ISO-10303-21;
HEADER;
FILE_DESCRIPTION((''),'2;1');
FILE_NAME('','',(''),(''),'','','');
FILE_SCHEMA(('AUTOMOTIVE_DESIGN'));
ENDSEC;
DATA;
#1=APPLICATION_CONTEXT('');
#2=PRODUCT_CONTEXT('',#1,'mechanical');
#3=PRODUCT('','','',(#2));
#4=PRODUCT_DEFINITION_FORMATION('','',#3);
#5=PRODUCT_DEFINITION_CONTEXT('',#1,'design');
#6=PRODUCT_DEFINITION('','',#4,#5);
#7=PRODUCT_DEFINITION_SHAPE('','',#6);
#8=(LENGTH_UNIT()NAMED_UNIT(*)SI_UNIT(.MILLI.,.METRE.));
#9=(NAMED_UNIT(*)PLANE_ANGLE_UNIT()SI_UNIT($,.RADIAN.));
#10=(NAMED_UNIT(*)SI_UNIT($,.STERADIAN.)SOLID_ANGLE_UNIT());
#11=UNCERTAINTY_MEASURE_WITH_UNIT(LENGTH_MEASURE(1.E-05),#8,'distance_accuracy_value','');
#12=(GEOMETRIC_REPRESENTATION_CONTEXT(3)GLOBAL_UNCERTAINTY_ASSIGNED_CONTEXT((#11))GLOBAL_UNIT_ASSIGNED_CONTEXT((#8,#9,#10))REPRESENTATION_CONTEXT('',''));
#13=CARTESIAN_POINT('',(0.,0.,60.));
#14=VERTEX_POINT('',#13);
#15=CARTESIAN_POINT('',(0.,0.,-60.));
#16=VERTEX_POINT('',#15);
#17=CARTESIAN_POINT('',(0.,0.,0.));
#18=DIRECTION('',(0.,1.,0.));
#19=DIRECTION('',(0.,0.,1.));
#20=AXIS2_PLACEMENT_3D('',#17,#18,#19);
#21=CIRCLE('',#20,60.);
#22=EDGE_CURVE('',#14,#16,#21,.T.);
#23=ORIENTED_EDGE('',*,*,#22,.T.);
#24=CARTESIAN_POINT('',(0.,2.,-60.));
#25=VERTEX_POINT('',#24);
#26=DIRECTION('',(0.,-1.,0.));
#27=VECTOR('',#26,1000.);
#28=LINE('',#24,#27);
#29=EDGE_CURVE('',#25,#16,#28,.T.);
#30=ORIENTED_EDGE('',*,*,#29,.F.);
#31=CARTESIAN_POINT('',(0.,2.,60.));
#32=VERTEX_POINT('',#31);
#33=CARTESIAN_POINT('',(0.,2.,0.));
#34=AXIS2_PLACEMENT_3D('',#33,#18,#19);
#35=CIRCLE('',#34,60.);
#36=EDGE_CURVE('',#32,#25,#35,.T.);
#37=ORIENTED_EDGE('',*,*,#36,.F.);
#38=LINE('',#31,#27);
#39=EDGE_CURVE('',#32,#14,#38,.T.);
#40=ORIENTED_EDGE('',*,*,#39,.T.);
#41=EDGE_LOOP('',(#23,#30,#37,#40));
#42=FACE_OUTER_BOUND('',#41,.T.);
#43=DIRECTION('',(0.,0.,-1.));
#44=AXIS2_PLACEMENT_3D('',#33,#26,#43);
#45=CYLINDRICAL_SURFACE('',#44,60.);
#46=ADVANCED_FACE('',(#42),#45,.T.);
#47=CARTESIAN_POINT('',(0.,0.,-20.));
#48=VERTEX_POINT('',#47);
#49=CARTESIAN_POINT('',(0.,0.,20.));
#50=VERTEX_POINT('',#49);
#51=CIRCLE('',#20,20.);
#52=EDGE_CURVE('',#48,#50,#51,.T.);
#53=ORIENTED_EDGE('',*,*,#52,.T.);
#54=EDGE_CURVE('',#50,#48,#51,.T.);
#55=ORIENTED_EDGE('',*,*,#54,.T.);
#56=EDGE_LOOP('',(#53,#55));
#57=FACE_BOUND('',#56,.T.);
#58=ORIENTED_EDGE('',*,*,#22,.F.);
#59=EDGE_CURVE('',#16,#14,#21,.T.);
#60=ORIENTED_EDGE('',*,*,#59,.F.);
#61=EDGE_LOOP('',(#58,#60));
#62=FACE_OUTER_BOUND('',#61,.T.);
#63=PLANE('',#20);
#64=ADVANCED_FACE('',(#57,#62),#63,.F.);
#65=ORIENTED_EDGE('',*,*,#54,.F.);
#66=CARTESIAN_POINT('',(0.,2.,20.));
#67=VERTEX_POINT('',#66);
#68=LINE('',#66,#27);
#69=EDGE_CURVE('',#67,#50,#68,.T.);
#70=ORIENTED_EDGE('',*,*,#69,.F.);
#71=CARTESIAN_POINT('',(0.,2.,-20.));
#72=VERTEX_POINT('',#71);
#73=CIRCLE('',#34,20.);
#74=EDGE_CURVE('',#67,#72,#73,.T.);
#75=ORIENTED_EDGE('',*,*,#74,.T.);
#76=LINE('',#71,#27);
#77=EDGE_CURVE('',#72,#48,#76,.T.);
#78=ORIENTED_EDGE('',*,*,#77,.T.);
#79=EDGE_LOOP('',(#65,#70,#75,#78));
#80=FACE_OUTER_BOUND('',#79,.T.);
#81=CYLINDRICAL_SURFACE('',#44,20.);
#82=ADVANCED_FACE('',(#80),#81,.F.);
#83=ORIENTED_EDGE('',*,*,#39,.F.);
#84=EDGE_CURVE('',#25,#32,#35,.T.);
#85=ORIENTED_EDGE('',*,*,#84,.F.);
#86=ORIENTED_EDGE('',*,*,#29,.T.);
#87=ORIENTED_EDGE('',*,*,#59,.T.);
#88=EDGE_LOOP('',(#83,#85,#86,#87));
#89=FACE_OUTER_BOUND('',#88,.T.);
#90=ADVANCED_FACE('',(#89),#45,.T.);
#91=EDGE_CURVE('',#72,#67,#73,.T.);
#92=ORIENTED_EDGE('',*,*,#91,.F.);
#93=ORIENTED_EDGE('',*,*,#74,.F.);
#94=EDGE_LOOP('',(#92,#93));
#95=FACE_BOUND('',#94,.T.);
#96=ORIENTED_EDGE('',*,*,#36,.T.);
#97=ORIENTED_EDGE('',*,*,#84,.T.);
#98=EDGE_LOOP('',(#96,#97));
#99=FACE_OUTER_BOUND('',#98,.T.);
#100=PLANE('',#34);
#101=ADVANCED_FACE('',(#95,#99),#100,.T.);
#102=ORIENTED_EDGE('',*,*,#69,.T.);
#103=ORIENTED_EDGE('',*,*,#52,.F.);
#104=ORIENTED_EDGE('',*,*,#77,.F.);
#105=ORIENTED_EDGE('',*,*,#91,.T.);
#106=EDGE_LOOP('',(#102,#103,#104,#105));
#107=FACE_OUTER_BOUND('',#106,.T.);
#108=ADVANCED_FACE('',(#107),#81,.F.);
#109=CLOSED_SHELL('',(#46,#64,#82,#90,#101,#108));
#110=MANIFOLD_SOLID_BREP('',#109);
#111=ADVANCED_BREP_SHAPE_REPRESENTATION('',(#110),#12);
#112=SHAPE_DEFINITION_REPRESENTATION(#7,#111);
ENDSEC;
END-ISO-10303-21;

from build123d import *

# Parameters (mm, degrees)
SKETCH1_R           = 60
SKETCH1_R_2         = 20
BOSS_EXTRUDE1_DEPTH = 2


with BuildPart() as part:
    # Sketch1 → Boss-Extrude1 (new body)
    with BuildSketch(Plane(origin=(0, 0, 0), x_dir=(1, 0, 0), z_dir=(0, 1, 0))):
        with Locations(Location((0, 0, 0), (0, 0, 270))):
            Circle(SKETCH1_R)
        with Locations(Location((0, 0, 0), (0, 0, 270))):
            Circle(SKETCH1_R_2, mode=Mode.SUBTRACT)
    extrude(amount=BOSS_EXTRUDE1_DEPTH)


solid = part.part
